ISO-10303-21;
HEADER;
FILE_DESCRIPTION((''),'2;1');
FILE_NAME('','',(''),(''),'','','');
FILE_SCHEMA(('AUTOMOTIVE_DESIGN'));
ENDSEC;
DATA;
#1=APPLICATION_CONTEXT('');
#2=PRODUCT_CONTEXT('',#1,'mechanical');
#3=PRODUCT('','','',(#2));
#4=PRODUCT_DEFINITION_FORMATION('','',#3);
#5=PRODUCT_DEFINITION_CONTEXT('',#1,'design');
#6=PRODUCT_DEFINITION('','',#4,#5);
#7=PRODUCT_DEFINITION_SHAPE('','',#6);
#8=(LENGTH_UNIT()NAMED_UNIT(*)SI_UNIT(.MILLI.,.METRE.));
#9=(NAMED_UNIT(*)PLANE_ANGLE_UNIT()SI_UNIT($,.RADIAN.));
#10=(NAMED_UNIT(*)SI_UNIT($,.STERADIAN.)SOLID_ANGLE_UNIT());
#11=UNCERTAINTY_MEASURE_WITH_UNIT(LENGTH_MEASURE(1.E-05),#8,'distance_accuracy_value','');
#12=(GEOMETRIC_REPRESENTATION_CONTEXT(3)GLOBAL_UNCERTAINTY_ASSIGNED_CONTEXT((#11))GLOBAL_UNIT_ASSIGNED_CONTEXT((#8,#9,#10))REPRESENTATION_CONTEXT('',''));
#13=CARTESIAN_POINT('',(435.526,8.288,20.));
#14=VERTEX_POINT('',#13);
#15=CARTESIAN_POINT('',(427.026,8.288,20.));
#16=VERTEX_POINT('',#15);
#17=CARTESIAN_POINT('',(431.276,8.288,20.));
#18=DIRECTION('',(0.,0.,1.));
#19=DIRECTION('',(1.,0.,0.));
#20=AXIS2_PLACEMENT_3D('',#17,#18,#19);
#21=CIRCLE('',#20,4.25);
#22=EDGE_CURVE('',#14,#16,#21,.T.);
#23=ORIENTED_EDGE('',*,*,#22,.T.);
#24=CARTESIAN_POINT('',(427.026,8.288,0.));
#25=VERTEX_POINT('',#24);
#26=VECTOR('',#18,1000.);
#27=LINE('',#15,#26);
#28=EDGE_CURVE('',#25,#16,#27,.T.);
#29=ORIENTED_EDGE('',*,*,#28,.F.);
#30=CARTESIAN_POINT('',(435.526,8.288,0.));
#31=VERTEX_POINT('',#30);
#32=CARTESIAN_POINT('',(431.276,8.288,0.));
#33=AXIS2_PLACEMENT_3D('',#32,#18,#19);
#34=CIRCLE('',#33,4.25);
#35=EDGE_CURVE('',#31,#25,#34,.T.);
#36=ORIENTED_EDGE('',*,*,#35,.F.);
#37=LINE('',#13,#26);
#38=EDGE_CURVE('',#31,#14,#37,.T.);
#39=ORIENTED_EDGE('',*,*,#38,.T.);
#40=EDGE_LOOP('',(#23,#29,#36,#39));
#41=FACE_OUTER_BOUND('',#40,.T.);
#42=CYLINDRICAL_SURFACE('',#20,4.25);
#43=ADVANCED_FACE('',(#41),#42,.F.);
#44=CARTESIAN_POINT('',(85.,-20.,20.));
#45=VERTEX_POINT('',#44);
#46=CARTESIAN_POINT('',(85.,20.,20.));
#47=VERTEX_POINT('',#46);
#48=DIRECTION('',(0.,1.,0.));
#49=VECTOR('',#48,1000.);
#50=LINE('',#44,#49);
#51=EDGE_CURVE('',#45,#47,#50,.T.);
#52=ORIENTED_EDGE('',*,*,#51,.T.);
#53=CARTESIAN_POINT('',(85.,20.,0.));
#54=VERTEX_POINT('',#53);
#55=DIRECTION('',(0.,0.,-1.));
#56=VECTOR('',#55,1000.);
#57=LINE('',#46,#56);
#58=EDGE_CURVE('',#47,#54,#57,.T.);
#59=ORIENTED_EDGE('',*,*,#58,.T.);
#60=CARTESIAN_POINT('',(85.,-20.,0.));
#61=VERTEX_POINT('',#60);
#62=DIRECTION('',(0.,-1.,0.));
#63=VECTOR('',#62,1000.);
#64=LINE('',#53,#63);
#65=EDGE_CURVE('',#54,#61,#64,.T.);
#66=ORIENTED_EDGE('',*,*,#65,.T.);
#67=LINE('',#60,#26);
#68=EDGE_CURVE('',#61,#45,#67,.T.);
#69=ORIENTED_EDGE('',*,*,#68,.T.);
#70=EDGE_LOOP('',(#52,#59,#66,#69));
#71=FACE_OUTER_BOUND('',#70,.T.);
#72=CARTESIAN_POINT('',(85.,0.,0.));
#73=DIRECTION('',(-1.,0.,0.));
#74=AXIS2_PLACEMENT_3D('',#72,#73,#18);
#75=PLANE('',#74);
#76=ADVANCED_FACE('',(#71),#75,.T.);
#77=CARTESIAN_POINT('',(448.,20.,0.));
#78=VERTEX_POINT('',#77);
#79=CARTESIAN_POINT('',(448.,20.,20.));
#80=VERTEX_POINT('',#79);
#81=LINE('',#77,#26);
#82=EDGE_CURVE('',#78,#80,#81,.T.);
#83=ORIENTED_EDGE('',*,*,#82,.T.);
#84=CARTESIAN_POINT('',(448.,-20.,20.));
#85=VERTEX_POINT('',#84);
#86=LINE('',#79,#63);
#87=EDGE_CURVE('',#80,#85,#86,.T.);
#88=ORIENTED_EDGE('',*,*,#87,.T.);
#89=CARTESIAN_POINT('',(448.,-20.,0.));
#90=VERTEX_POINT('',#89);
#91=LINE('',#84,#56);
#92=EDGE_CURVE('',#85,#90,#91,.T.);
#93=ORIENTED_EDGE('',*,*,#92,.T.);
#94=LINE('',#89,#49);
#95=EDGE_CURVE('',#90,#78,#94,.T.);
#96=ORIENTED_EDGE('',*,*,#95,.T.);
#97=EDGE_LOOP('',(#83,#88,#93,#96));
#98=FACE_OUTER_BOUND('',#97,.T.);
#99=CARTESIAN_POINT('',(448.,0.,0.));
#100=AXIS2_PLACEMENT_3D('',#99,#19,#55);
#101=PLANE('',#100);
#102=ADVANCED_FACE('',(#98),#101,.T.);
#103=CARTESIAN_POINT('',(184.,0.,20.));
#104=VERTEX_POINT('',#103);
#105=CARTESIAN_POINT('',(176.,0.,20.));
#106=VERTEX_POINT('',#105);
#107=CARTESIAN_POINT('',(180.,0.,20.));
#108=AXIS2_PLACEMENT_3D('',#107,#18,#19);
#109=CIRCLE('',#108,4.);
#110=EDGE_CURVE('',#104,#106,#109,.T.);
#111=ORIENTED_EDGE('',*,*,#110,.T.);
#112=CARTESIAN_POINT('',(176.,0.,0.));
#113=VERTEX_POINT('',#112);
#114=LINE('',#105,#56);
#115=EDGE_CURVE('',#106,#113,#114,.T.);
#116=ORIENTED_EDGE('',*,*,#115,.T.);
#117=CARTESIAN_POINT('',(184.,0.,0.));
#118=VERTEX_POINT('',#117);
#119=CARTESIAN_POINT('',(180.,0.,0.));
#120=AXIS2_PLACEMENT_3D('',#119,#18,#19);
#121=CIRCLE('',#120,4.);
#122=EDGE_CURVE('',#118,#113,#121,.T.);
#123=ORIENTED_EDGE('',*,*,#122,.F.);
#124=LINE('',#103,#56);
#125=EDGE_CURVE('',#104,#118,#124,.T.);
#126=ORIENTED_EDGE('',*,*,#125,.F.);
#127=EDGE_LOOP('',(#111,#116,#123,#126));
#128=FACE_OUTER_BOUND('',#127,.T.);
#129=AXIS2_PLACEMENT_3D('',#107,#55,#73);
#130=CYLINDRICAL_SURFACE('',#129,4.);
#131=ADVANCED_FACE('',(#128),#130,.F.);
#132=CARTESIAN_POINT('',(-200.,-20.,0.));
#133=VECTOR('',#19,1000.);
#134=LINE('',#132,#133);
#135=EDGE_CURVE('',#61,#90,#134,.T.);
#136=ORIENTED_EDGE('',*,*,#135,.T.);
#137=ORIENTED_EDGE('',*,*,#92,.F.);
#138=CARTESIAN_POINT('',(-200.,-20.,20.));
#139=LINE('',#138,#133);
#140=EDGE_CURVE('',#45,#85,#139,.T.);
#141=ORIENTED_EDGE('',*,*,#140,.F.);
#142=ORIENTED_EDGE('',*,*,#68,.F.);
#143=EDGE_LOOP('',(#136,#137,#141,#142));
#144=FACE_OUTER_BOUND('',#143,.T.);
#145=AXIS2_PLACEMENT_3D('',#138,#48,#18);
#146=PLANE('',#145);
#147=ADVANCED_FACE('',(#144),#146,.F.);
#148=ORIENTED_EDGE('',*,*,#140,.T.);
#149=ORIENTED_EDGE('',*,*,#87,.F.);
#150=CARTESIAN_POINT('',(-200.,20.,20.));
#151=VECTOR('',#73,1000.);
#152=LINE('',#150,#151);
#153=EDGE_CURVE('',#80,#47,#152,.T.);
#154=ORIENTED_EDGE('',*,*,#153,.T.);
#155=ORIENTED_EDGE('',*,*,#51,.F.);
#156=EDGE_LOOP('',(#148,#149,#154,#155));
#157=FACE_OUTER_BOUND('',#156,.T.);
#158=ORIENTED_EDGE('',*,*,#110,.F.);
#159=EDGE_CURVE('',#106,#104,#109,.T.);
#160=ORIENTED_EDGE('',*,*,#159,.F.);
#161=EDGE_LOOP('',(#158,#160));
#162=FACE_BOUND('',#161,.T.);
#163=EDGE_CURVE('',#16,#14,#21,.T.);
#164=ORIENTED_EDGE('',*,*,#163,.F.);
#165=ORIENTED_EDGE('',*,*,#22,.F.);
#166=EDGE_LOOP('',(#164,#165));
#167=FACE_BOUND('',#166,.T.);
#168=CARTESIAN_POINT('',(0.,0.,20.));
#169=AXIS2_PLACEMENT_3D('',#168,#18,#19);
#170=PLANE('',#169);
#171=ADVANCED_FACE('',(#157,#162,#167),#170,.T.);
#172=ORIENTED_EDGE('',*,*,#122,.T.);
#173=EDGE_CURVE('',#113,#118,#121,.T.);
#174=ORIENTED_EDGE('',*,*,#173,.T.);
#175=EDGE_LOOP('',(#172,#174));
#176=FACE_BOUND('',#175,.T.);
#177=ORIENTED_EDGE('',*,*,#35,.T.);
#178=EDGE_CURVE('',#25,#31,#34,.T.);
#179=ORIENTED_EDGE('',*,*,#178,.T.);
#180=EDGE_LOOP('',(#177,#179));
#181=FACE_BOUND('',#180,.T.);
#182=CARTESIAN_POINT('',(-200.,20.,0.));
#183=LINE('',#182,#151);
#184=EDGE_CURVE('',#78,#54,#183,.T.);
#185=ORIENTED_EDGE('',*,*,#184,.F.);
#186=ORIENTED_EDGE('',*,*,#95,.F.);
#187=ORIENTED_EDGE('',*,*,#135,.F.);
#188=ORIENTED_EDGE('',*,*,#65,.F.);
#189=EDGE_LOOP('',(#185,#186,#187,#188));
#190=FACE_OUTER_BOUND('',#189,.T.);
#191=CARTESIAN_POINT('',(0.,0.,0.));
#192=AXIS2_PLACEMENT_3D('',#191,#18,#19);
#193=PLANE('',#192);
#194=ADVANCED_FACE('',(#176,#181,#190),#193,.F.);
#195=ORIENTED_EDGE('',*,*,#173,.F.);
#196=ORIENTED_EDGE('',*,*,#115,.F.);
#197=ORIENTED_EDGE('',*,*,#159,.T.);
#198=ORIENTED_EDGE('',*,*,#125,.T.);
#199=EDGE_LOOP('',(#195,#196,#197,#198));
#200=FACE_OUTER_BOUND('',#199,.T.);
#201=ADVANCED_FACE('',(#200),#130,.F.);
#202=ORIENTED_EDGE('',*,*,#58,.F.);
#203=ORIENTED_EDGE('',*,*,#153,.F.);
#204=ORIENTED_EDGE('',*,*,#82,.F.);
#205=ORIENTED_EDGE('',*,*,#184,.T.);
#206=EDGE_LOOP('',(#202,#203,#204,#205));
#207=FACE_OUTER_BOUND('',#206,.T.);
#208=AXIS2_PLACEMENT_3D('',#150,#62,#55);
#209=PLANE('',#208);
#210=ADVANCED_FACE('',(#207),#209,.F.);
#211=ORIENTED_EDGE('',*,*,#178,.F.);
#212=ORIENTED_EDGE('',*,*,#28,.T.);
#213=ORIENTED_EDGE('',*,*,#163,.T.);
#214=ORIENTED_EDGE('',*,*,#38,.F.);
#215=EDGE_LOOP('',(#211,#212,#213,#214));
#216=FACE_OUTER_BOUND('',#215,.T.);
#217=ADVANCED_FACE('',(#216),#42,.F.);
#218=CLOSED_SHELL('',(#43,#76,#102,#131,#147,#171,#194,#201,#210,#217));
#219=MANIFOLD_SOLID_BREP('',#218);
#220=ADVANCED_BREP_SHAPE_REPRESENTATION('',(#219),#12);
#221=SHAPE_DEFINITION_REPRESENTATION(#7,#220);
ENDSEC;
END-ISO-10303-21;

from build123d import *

# Parameters (mm, degrees)
SKETCH_2_W          = 400
SKETCH_2_H          = 40
SKETCH_2_R          = 4
EXTRUDE_1_DEPTH     = 20
SKETCH_4_W          = 20
SKETCH_4_H          = 40
EXTRUDE_2_DEPTH     = 248
HOLE_WIZARD_M10_1_D = 8.5
SKETCH_9_W          = 20
SKETCH_9_H          = 40
CUT_EXTRUDE_2_DEPTH = 285


with BuildPart() as part:
    # 草图2 → 凸台-拉伸1 (new body)
    with BuildSketch(Plane.XY):
        Rectangle(SKETCH_2_W, SKETCH_2_H)
        with Locations((180, 0)):
            Circle(SKETCH_2_R, mode=Mode.SUBTRACT)
    extrude(amount=EXTRUDE_1_DEPTH)

    # 草图4 → 凸台-拉伸2 (add)
    with BuildSketch(Plane(origin=(200, 0, 0), x_dir=(0, 0, -1), z_dir=(1, 0, 0))):
        with Locations((-10, 0)):
            Rectangle(SKETCH_4_W, SKETCH_4_H)
    extrude(amount=EXTRUDE_2_DEPTH)

    # M10 螺纹孔1 (through all)
    with Locations(Plane.XY.offset(20)):
        with Locations((431.276, 8.288)):
            Hole(HOLE_WIZARD_M10_1_D / 2)

    # 草图9 → 切除-拉伸2 (cut)
    with BuildSketch(Plane.ZY.offset(200)):
        with Locations((10, 0)):
            Rectangle(SKETCH_9_W, SKETCH_9_H)
    extrude(amount=-CUT_EXTRUDE_2_DEPTH, mode=Mode.SUBTRACT)


solid = part.part
